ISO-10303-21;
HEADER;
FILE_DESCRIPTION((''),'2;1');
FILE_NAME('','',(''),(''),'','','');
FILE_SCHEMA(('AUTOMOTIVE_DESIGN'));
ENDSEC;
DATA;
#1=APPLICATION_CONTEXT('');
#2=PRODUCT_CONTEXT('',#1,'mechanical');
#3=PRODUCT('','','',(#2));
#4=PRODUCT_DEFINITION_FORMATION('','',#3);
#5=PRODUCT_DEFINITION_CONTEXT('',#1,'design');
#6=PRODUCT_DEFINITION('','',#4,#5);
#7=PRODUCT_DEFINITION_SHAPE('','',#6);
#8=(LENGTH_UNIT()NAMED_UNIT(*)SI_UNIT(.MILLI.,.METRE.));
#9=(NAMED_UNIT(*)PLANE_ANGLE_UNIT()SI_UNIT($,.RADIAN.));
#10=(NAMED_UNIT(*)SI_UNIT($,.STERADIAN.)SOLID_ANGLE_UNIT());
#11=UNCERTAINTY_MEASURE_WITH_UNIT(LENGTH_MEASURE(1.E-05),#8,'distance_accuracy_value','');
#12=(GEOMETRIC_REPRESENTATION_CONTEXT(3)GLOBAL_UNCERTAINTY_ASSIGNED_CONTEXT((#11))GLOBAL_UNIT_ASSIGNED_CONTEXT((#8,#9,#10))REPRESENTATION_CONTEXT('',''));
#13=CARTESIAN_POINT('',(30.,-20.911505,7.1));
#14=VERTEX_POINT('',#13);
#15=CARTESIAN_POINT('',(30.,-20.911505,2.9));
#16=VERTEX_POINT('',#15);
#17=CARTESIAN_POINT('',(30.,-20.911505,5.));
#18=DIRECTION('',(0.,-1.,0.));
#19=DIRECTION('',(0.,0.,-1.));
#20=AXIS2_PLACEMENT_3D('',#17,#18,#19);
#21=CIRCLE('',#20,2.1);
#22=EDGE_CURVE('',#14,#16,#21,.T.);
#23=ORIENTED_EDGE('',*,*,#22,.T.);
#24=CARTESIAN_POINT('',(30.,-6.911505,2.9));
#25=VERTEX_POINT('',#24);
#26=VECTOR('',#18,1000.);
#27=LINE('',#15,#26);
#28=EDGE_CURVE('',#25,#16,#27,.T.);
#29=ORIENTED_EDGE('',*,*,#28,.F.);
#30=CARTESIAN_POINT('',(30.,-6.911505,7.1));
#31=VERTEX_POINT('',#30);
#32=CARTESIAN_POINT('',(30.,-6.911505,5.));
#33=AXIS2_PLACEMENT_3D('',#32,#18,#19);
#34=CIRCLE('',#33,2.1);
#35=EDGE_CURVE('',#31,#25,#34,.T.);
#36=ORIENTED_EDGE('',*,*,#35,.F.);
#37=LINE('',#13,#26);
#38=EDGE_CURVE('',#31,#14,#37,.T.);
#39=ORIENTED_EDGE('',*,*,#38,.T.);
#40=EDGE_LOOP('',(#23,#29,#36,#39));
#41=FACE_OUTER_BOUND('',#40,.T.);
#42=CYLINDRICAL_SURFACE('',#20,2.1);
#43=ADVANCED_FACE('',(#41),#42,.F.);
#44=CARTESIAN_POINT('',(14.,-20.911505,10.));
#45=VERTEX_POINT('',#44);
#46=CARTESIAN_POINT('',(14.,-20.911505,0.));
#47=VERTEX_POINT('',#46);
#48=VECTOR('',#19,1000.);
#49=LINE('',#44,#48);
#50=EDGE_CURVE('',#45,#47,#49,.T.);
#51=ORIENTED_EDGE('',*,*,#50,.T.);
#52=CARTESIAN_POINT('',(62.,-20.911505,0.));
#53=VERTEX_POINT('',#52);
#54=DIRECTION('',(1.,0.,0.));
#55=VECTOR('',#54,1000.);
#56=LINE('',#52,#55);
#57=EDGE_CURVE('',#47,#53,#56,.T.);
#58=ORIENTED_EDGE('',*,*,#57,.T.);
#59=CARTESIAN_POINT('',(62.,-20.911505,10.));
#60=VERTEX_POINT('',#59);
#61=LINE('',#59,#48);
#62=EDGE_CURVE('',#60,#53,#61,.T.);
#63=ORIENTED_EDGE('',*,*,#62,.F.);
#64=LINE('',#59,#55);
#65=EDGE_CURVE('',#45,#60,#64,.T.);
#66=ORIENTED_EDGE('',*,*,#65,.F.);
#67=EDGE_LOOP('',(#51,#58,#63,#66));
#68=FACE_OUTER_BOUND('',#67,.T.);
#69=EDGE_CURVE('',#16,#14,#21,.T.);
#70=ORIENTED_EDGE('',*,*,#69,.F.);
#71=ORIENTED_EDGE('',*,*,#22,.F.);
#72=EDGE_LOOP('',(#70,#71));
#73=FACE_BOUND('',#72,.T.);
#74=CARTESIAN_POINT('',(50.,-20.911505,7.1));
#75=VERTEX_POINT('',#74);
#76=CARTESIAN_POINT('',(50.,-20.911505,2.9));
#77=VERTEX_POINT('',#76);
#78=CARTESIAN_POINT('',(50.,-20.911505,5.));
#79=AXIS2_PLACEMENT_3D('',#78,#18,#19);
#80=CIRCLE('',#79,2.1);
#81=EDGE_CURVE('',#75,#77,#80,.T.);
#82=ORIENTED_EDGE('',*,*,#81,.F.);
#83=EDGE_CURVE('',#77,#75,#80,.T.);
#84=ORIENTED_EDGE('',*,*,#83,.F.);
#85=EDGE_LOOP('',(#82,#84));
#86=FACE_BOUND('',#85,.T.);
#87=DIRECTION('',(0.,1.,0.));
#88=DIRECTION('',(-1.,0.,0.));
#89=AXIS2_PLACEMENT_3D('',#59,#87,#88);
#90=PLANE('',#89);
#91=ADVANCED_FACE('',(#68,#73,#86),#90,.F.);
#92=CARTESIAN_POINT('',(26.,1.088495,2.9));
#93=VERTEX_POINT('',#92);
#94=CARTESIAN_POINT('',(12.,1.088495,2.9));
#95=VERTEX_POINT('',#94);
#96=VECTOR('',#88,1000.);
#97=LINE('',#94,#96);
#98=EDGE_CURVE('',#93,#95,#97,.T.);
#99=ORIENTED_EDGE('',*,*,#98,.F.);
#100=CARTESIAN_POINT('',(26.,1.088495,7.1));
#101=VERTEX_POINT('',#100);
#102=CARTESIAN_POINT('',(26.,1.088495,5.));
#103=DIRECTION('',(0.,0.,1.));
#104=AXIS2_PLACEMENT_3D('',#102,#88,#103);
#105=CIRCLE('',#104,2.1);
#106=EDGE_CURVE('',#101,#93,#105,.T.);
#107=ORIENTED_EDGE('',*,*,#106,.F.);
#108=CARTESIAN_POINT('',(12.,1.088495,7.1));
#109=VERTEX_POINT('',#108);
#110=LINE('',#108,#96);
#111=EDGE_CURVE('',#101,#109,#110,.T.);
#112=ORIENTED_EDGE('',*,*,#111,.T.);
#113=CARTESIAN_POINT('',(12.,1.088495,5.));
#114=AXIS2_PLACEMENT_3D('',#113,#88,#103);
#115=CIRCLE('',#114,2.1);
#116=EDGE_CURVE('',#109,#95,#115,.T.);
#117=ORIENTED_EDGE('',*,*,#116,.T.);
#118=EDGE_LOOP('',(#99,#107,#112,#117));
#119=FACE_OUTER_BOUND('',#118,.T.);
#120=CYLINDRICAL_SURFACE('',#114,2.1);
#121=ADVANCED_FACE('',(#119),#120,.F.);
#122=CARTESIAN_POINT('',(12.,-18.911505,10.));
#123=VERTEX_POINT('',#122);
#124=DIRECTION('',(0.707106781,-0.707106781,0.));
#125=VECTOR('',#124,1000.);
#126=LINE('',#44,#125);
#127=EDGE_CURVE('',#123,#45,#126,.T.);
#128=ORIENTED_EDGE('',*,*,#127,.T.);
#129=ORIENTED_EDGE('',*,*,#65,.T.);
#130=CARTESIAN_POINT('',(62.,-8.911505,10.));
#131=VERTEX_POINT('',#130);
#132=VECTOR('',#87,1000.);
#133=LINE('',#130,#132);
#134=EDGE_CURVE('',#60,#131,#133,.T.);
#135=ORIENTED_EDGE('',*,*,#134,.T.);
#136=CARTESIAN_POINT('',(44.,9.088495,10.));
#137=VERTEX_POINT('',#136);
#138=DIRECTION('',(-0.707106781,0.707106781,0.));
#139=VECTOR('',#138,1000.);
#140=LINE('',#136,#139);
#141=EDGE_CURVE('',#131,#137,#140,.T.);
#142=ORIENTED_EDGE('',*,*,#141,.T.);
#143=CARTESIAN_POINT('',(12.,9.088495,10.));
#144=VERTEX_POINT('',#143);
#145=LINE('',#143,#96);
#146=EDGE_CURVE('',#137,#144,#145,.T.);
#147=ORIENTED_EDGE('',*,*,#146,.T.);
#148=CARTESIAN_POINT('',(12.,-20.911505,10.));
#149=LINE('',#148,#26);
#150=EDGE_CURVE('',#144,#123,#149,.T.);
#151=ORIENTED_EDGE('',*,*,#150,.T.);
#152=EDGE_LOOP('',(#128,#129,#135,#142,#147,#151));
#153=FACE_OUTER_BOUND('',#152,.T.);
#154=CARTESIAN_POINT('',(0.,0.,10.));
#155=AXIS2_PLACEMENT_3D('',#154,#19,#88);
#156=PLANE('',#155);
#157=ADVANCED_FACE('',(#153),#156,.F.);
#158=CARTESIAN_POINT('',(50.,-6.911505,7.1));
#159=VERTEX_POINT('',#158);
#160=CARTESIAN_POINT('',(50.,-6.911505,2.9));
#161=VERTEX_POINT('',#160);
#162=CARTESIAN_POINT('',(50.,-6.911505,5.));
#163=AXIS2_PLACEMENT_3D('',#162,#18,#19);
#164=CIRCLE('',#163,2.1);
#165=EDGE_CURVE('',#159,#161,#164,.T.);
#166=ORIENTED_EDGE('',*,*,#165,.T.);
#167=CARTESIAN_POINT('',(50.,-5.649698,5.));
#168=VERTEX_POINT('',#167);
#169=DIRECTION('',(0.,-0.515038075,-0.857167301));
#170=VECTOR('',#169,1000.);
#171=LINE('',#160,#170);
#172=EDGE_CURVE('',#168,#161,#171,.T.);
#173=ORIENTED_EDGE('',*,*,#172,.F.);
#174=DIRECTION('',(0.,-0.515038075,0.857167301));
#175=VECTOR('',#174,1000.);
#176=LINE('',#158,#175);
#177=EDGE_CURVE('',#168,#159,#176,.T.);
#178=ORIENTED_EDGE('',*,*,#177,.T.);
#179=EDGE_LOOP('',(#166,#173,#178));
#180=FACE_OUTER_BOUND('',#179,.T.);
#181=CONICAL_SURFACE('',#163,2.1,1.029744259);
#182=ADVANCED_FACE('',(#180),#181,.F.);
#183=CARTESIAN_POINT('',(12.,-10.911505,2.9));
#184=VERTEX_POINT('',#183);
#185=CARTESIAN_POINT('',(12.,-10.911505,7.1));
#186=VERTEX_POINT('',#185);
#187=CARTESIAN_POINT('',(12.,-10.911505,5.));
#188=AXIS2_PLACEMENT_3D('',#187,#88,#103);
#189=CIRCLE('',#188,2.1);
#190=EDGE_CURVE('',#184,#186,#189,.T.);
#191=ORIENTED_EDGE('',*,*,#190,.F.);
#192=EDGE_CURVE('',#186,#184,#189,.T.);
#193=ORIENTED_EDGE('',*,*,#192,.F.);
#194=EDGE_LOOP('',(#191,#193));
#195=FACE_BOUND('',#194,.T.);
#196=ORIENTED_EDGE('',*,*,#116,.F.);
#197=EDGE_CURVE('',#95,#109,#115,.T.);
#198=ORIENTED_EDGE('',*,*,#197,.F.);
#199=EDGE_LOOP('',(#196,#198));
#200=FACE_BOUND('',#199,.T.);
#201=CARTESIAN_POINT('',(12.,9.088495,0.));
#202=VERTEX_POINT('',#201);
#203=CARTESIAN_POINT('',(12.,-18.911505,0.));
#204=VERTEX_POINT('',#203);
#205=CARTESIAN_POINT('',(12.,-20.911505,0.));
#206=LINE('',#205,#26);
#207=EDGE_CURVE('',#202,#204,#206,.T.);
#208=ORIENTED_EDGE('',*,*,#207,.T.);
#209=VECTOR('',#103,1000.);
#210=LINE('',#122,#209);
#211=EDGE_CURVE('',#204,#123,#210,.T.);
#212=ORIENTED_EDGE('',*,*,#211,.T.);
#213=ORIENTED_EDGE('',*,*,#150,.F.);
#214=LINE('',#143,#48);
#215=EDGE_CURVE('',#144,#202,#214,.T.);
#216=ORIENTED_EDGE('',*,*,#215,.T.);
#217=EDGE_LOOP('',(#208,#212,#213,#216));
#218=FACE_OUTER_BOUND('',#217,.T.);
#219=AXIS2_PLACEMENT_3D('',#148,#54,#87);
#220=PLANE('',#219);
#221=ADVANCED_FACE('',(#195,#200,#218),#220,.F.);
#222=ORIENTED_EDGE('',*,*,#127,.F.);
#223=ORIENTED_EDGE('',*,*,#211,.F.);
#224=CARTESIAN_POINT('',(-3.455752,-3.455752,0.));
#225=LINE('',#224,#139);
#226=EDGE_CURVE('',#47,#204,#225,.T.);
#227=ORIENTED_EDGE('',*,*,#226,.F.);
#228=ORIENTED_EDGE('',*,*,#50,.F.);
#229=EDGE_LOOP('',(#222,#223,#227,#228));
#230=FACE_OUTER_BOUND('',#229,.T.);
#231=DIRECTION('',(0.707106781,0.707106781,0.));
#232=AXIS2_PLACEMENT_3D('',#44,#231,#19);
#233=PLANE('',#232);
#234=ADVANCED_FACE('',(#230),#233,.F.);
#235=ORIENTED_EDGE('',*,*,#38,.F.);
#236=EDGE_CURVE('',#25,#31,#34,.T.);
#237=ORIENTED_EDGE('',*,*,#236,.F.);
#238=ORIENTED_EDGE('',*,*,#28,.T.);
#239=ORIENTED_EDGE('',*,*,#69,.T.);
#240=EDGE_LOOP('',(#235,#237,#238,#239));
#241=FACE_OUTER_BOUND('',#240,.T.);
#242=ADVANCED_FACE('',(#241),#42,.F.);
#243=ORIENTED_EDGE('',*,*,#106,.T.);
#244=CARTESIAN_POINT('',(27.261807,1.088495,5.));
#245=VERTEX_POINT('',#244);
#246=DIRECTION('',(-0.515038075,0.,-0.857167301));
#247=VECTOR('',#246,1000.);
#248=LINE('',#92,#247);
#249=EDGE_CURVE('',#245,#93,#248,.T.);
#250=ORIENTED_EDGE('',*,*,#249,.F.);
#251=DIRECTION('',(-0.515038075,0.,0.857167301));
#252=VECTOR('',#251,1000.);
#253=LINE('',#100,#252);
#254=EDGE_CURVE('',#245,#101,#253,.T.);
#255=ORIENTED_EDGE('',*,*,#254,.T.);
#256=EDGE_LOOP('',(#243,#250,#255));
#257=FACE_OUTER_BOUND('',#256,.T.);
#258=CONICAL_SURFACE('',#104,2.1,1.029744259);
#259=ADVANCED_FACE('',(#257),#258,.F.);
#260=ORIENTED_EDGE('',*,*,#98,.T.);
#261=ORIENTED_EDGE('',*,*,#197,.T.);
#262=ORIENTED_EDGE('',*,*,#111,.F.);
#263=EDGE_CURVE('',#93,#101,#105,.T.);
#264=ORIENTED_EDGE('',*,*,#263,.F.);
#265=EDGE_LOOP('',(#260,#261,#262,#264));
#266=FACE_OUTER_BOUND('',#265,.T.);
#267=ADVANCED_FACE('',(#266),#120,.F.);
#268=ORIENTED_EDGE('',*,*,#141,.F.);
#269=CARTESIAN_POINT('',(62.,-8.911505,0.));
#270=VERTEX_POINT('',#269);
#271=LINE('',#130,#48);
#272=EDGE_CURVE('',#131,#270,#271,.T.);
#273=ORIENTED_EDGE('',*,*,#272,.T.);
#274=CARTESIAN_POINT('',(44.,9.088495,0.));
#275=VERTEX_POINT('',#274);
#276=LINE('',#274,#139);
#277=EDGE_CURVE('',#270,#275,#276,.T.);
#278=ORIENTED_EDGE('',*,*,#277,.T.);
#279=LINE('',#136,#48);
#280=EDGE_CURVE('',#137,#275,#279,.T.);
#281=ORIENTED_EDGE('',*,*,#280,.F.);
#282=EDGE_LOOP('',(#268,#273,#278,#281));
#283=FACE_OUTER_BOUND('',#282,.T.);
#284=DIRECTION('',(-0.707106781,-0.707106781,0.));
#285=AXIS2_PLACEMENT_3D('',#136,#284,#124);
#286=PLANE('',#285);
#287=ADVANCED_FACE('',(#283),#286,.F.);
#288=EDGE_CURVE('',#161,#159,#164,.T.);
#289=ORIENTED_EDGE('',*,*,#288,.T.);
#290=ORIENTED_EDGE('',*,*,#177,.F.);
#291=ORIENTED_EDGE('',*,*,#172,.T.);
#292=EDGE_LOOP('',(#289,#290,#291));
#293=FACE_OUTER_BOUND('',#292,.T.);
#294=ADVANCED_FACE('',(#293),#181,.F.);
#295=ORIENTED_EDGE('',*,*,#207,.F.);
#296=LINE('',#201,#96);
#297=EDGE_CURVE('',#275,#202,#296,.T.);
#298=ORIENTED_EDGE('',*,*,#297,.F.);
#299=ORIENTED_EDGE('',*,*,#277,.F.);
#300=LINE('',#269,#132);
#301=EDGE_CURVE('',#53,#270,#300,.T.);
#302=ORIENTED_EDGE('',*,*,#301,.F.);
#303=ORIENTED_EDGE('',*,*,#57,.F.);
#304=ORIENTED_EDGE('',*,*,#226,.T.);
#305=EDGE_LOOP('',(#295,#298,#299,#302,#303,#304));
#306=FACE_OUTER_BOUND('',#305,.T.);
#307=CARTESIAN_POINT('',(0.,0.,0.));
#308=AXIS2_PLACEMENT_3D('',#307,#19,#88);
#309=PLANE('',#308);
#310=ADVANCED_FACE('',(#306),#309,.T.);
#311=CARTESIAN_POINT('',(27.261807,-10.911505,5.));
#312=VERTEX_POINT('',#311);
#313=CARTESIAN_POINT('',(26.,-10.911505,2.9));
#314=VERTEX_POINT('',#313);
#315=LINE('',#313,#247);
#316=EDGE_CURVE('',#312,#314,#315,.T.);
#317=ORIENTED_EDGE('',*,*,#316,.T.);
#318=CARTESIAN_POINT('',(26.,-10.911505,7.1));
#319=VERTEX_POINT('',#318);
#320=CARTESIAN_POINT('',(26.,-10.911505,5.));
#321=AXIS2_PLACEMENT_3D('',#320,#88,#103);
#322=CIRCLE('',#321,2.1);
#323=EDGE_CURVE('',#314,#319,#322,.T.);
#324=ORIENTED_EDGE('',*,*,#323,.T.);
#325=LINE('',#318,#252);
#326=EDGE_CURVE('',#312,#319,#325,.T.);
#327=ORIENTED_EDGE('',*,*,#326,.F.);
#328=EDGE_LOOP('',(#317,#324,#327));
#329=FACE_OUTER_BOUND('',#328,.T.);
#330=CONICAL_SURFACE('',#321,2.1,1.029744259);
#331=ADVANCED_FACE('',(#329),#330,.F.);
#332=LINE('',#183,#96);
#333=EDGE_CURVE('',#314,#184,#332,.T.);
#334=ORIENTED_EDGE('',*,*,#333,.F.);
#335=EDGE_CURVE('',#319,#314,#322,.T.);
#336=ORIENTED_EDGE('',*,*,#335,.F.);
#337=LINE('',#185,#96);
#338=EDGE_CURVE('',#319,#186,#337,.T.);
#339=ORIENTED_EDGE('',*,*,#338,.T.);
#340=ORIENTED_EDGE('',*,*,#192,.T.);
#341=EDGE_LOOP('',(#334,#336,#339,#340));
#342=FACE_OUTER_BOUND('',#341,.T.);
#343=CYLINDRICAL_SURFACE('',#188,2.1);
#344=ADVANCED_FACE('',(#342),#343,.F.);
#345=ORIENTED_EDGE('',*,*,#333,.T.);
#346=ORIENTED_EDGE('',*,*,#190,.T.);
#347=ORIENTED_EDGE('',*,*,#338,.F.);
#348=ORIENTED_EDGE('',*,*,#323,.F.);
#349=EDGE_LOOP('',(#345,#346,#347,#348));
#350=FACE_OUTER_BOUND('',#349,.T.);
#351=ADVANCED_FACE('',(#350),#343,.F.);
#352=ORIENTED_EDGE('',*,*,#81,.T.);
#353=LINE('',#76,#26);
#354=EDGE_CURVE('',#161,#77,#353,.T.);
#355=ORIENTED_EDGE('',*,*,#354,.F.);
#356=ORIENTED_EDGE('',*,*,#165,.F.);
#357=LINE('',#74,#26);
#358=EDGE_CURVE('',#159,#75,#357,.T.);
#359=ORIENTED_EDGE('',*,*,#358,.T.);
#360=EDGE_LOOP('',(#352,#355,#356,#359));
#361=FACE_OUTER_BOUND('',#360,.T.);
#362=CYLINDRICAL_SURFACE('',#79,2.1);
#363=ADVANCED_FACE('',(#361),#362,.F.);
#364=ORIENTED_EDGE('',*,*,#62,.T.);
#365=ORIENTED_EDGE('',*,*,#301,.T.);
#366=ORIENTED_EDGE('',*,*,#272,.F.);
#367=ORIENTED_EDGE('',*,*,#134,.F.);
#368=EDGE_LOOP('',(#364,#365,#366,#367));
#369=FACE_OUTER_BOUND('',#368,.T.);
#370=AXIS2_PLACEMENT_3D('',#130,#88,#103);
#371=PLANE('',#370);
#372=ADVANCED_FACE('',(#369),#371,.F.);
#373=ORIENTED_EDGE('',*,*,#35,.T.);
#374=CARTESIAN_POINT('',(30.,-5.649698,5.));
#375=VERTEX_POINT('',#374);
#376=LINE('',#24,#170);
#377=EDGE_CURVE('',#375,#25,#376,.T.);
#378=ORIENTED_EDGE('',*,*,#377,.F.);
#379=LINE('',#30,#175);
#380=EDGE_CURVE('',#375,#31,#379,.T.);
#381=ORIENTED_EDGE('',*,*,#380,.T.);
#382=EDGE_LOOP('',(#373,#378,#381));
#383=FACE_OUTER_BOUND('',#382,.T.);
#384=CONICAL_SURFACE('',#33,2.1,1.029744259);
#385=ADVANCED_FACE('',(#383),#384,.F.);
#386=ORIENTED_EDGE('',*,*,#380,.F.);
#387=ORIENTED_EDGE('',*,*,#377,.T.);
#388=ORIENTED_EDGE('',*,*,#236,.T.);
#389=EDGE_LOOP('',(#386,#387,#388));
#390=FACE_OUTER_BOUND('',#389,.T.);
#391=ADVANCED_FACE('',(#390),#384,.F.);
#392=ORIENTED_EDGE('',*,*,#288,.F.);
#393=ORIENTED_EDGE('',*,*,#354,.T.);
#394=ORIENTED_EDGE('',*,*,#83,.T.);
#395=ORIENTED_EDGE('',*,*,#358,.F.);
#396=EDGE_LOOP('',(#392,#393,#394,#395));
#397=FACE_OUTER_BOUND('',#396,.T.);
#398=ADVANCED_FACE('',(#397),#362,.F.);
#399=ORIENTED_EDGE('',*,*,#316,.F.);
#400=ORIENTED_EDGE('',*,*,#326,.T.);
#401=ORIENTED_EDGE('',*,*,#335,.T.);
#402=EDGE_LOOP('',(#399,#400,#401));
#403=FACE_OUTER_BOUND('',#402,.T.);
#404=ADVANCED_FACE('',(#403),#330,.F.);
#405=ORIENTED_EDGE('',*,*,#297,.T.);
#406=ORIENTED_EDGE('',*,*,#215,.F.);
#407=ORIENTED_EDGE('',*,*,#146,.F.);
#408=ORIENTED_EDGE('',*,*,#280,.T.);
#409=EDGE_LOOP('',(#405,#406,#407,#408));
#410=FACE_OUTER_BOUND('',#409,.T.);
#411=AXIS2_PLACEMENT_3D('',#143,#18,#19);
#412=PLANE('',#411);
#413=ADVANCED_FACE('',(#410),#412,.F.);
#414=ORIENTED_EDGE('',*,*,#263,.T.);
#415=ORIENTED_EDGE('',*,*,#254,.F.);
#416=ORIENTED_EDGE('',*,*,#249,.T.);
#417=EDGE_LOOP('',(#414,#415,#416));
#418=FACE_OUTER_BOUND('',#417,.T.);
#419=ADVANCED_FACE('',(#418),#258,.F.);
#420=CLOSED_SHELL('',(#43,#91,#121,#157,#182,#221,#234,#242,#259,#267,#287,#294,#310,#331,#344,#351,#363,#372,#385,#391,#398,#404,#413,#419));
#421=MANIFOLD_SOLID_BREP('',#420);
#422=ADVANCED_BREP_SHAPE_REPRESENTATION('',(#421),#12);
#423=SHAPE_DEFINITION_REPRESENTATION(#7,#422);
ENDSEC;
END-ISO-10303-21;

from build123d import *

# Parameters (mm, degrees)
EXTRUDE_1_DEPTH        = 10
CHAMFER_1_SIZE         = 2
HOLE_WIZARD_M5_1_D     = 4.2
HOLE_WIZARD_M5_1_DEPTH = 14
HOLE_WIZARD_M5_1_TIP   = 1.2618073
HOLE_WIZARD_M5_2_D     = 4.2
HOLE_WIZARD_M5_2_DEPTH = 14
HOLE_WIZARD_M5_2_TIP   = 1.2618073


with BuildPart() as part:
    # 草图1 → 凸台-拉伸1 (new body)
    with BuildSketch(Plane.XY):
        Polygon((62, -20.911504847), (12, -20.911504847), (12, 9.088495153), (44, 9.088495153), (62, -8.911504847), align=None)
    extrude(amount=EXTRUDE_1_DEPTH)

    # 倒角1
    chamfer_1_edges = [part.edges().sort_by_distance(p)[0] for p in [
        (12, -20.911504847, 5),
    ]]
    chamfer(chamfer_1_edges, length=CHAMFER_1_SIZE)

    # M5 螺纹孔1
    with Locations(Plane.ZY.offset(-12)):
        with Locations((5, -10.911504847), (5, 1.088495153)):
            Hole(HOLE_WIZARD_M5_1_D / 2, depth=HOLE_WIZARD_M5_1_DEPTH)
            with Locations((0, 0, -(HOLE_WIZARD_M5_1_DEPTH + HOLE_WIZARD_M5_1_TIP / 2))):  # 118° drill point
                Cone(0, HOLE_WIZARD_M5_1_D / 2, HOLE_WIZARD_M5_1_TIP, mode=Mode.SUBTRACT)

    # M5 螺纹孔2
    with Locations(Plane(origin=(0, -20.911504847, 0), x_dir=(-1, 0, 0), z_dir=(0, -1, 0))):
        with Locations((-30, -5), (-50, -5)):
            Hole(HOLE_WIZARD_M5_2_D / 2, depth=HOLE_WIZARD_M5_2_DEPTH)
            with Locations((0, 0, -(HOLE_WIZARD_M5_2_DEPTH + HOLE_WIZARD_M5_2_TIP / 2))):  # 118° drill point
                Cone(0, HOLE_WIZARD_M5_2_D / 2, HOLE_WIZARD_M5_2_TIP, mode=Mode.SUBTRACT)


solid = part.part
